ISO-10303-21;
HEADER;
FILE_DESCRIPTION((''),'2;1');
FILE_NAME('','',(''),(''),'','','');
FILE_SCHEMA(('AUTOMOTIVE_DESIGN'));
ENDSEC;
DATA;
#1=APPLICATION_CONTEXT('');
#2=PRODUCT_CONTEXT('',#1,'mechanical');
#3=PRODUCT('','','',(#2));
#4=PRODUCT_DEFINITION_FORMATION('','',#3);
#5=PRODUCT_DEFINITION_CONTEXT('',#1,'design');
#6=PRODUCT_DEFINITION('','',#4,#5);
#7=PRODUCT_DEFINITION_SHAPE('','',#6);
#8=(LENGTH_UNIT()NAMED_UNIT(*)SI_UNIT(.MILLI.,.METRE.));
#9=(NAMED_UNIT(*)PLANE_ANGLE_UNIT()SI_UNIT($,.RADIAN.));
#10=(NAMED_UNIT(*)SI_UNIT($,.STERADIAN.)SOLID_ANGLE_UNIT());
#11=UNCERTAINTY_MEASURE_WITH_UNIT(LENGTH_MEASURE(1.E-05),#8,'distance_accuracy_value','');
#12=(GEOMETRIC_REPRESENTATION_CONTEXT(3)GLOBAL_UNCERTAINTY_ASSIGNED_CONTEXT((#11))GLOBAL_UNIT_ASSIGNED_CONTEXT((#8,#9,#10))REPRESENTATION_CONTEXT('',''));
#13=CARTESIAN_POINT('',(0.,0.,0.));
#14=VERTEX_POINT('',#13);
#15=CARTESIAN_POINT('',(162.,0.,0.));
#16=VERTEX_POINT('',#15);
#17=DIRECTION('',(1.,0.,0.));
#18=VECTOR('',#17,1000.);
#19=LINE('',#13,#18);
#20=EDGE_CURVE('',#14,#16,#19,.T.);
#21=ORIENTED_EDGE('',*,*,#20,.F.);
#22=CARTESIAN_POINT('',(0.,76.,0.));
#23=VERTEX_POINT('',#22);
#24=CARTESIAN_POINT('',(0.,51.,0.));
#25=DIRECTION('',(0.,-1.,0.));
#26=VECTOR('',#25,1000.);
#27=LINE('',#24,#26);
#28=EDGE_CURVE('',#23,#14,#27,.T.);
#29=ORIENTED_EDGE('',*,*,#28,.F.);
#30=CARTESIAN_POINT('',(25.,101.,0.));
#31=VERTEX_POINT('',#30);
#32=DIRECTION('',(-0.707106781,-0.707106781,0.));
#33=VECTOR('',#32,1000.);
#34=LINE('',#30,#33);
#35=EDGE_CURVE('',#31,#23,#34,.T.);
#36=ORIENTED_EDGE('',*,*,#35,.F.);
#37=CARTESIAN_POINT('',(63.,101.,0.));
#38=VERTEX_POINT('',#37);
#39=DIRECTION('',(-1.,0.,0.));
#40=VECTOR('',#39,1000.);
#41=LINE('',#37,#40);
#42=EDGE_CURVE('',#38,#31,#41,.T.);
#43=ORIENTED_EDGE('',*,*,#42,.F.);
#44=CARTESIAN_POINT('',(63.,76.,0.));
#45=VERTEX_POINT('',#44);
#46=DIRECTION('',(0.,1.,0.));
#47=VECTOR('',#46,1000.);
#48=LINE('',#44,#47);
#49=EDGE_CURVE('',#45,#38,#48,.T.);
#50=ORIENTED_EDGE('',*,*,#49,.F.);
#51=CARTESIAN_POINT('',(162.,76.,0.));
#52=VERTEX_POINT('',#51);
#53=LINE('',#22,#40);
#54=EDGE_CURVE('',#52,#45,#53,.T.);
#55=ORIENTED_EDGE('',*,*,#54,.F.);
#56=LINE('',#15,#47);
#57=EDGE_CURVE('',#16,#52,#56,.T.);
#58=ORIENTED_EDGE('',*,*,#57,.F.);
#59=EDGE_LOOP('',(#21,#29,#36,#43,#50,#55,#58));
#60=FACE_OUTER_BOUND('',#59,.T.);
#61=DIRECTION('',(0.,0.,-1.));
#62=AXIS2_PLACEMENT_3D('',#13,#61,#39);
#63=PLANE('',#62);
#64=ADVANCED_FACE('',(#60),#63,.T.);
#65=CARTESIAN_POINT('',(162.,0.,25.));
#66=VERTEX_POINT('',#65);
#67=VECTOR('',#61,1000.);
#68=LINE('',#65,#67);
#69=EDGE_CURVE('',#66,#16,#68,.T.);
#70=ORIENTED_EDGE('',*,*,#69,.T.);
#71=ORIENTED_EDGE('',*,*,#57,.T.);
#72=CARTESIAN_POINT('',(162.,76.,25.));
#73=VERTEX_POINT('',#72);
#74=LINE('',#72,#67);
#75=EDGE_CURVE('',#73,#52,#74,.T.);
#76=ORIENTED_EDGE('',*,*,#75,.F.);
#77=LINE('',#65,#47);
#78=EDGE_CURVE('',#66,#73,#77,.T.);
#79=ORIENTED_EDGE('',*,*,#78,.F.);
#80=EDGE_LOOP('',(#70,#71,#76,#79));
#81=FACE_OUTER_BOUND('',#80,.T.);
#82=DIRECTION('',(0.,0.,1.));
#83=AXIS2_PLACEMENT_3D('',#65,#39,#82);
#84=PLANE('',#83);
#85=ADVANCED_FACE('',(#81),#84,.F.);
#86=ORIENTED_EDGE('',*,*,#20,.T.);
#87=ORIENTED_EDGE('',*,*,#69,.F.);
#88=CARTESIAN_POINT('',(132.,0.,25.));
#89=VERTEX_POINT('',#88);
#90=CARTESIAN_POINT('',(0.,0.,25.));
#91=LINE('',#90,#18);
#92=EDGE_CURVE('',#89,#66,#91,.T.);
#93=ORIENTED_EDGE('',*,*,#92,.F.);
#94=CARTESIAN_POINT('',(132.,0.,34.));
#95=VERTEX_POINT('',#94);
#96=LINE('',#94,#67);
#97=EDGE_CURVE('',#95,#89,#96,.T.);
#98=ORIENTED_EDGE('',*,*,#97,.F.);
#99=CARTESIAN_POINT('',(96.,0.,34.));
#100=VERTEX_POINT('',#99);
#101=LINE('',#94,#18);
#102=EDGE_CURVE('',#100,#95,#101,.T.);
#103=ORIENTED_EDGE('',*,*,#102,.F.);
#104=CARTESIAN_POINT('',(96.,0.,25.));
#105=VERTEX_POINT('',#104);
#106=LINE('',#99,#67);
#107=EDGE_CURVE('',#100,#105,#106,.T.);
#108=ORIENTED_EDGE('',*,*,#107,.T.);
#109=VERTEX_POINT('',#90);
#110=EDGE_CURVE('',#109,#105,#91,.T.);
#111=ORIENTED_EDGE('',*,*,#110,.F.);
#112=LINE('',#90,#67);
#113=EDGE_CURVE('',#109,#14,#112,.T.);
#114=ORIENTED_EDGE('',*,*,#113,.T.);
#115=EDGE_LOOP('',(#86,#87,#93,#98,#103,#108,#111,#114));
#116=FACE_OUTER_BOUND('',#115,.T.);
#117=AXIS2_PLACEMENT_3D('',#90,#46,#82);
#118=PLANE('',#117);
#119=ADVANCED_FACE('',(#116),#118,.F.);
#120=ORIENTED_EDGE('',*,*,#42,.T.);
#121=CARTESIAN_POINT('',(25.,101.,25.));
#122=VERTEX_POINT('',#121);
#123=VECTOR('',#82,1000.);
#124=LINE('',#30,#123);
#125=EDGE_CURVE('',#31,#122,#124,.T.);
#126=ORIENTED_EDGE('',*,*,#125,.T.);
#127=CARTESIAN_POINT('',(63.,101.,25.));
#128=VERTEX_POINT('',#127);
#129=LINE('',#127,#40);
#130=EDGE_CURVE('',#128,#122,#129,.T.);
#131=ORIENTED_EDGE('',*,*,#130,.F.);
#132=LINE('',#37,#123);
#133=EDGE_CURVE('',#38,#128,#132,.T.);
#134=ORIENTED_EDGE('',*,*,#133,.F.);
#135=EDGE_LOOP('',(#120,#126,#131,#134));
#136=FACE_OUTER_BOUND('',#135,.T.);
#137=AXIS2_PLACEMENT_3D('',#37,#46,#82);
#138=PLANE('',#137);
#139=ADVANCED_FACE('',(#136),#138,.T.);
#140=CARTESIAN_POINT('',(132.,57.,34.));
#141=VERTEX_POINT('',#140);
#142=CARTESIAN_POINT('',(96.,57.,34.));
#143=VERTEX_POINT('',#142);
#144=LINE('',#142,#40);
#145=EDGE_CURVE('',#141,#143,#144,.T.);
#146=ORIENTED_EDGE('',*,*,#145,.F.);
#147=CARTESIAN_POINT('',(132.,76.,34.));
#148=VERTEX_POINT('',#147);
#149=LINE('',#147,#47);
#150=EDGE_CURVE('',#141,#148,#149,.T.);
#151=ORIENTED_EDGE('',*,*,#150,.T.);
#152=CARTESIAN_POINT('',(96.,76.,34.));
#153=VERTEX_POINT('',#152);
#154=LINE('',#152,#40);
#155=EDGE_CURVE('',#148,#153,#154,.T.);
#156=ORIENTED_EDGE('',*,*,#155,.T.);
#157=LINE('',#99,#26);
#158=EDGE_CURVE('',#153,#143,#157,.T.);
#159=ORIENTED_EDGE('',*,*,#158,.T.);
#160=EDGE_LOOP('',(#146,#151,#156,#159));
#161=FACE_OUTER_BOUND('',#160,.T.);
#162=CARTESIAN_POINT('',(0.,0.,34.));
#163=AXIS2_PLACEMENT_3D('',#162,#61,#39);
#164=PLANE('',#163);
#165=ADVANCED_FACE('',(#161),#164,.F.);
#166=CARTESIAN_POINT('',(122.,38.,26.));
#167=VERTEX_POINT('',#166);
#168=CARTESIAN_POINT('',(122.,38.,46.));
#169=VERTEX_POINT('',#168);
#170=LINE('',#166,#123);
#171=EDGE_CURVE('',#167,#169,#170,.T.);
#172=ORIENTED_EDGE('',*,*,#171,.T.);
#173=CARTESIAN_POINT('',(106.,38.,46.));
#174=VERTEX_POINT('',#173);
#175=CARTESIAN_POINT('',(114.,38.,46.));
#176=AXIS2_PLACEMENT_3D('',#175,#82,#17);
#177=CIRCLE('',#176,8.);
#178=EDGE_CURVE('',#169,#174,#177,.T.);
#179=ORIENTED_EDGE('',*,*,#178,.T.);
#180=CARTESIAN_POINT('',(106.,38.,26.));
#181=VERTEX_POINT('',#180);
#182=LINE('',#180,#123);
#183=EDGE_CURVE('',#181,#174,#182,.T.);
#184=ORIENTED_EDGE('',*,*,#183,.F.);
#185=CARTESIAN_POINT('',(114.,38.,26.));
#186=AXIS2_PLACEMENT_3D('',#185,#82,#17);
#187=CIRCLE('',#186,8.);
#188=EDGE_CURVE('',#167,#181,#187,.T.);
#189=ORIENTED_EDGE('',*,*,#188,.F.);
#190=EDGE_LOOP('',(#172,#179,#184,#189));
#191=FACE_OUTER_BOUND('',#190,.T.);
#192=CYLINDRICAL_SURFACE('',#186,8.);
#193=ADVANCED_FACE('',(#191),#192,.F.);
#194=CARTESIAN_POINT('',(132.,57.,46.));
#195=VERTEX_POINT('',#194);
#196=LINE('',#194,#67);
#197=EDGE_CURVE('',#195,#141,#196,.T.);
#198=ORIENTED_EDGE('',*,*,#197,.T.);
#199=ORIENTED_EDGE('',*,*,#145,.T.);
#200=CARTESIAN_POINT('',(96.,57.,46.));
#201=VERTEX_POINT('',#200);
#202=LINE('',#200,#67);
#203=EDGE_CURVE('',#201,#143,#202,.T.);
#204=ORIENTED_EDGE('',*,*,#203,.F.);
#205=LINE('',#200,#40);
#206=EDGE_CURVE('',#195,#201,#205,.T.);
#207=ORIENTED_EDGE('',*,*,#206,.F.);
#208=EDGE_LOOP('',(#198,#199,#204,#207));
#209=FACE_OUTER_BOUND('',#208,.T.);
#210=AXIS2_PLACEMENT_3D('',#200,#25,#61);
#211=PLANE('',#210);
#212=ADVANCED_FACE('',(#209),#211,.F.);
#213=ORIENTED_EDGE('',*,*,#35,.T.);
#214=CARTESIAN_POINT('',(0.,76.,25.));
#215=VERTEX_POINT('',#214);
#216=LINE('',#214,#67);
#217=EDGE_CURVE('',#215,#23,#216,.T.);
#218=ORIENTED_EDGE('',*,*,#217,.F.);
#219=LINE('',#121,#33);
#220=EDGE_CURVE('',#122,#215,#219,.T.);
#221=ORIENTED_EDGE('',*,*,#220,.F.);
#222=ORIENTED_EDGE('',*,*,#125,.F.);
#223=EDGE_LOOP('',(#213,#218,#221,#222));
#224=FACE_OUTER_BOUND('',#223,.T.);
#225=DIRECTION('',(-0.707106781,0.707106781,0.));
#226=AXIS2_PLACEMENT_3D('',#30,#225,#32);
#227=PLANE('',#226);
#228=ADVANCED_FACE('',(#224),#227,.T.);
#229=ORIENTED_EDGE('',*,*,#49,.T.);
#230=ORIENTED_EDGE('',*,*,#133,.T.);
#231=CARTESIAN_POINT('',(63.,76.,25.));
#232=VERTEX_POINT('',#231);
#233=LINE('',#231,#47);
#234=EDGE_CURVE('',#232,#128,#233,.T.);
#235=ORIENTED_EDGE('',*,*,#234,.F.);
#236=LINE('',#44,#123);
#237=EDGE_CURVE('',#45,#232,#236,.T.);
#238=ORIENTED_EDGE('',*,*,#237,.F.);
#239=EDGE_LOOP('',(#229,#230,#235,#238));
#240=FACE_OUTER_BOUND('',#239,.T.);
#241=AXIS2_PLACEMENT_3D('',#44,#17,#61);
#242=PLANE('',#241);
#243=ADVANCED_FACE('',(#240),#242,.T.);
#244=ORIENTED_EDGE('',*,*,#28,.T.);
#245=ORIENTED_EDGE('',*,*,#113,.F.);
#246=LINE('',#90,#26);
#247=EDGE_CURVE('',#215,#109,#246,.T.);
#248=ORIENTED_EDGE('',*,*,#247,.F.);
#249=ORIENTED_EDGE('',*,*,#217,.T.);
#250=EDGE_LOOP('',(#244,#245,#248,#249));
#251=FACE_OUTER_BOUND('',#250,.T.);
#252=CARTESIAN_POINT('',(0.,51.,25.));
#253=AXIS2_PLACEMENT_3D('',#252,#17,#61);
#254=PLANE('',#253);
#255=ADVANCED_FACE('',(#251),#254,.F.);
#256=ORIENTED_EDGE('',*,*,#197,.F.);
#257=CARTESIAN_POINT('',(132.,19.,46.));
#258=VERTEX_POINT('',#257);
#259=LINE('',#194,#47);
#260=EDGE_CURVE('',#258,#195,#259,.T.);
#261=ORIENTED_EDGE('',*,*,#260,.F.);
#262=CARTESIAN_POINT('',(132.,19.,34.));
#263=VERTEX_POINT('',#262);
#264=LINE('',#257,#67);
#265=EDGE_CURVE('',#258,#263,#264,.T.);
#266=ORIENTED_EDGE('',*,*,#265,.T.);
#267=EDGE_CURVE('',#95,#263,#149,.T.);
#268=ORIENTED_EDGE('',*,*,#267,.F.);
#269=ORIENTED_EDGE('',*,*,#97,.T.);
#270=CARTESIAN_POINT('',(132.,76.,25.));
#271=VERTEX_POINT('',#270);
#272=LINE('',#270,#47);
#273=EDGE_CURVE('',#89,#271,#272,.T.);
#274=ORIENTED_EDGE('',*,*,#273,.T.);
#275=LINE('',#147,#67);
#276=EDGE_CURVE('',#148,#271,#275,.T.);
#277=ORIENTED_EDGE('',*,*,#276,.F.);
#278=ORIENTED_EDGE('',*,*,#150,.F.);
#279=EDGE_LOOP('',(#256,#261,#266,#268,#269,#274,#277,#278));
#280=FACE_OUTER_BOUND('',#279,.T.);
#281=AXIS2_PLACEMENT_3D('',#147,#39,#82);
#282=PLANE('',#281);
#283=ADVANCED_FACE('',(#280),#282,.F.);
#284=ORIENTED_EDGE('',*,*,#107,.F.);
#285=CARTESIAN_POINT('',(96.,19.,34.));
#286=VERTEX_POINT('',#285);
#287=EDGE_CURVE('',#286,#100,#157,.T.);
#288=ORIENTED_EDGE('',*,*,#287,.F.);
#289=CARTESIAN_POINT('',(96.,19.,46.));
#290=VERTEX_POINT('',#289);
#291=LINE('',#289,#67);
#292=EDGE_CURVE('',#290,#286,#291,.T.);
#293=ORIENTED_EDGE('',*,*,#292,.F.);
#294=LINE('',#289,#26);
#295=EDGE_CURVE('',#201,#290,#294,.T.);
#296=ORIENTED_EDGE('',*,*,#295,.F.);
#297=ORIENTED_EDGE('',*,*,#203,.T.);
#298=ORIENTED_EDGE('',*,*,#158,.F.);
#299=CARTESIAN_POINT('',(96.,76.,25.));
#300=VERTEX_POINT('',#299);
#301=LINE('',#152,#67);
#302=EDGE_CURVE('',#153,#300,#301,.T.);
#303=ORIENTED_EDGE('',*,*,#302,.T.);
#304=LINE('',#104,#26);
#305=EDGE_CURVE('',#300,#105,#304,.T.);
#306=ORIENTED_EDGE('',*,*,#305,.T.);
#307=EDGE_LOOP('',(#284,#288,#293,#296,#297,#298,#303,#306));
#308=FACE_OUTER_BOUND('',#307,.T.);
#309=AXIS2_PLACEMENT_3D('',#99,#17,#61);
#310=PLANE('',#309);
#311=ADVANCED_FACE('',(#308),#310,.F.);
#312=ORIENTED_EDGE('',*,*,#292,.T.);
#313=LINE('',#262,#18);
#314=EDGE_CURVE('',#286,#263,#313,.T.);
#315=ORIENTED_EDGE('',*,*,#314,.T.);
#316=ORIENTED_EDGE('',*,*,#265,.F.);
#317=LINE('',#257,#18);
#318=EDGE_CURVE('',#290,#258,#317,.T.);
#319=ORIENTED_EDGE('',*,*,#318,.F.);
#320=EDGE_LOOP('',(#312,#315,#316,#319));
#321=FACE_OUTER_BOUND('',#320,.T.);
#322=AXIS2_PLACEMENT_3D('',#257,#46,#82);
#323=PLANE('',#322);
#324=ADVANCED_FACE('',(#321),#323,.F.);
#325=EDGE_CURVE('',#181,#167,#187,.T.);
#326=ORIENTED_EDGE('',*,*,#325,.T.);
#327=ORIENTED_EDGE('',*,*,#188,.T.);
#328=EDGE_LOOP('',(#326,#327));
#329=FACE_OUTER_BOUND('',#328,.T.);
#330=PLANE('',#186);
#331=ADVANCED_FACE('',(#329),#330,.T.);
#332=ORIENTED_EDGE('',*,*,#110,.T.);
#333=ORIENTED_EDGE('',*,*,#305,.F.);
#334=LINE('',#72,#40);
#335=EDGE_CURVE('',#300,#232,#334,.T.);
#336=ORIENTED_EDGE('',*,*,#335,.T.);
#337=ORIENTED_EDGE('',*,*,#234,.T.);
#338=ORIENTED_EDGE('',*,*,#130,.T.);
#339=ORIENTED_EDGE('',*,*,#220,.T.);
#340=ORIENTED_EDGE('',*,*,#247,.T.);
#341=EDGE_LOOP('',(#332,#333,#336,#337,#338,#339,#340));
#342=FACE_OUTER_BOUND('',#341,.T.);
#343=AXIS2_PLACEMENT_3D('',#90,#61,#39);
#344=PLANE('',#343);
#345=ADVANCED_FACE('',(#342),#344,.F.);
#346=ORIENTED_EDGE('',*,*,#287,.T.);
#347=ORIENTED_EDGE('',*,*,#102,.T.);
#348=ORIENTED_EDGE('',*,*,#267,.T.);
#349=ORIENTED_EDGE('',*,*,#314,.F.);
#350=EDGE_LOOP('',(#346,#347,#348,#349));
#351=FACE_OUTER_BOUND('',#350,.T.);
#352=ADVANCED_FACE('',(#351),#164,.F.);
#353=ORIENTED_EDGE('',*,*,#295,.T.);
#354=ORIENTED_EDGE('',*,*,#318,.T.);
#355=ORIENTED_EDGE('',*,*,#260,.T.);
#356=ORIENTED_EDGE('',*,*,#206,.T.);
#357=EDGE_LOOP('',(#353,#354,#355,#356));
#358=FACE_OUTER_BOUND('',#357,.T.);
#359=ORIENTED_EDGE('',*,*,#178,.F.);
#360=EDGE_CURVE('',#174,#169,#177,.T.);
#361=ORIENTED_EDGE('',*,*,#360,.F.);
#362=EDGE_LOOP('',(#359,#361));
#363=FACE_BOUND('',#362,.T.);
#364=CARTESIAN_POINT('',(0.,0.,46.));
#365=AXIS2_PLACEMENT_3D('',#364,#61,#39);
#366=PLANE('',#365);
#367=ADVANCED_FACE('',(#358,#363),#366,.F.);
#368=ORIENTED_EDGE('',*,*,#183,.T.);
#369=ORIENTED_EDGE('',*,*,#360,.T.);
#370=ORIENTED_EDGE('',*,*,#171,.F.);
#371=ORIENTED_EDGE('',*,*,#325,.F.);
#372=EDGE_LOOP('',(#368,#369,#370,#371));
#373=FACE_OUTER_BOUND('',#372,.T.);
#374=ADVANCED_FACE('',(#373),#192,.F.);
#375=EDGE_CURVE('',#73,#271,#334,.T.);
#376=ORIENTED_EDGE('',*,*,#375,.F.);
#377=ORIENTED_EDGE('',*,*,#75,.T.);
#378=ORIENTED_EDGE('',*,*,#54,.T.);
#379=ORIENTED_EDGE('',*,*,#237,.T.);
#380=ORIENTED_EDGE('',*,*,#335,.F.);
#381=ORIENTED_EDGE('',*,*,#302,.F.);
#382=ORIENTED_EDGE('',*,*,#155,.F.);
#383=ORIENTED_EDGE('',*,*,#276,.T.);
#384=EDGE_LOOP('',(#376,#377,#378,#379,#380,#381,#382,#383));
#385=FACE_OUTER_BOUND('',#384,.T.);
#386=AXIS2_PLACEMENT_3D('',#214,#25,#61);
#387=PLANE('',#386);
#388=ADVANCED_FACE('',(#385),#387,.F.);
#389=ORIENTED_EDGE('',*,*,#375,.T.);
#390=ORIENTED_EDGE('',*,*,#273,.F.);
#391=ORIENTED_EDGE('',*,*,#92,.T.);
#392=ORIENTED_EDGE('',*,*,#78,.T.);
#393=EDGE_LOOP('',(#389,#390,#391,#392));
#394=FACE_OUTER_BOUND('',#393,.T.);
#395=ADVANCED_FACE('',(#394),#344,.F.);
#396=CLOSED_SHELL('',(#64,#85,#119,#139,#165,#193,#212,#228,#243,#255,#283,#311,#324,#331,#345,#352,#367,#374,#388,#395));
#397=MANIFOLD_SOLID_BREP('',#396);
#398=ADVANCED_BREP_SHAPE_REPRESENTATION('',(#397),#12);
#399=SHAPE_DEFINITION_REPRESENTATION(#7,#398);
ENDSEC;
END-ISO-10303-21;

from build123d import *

# Parameters (mm, degrees)
BASE_BLOCK_DEPTH   = 25
SIDE_BLOCK_DEPTH   = 25
PAD_SKETCH_W       = 36
PAD_SKETCH_H       = 76
MOUNTING_PAD_DEPTH = 9
LUG_BOSS_SKETCH_W  = 36
LUG_BOSS_SKETCH_H  = 38
LUG_BOSS_DEPTH     = 12
HOLE_SKETCH_16_R   = 8
HOLE_16_DEPTH      = 20


with BuildPart() as part:
    # Base Profile Sketch → Base Block (new body)
    with BuildSketch(Plane.XY):
        Polygon((0, 0), (162, 0), (162, 76), (25, 76), (0, 76), (0, 51), align=None)
    extrude(amount=BASE_BLOCK_DEPTH)

    # Side Block Sketch → Side Block (add)
    with BuildSketch(Plane.XY.offset(25)):
        Polygon((63, 76), (63, 101), (25, 101), (0, 76), (25, 76), align=None)
    extrude(amount=-SIDE_BLOCK_DEPTH)

    # Pad Sketch → Mounting Pad (add)
    with BuildSketch(Plane.XY.offset(25)):
        with Locations((114, 38)):
            Rectangle(PAD_SKETCH_W, PAD_SKETCH_H)
    extrude(amount=MOUNTING_PAD_DEPTH)

    # Lug Boss Sketch → Lug Boss (add)
    with BuildSketch(Plane.XY.offset(34)):
        with Locations((114, 38)):
            Rectangle(LUG_BOSS_SKETCH_W, LUG_BOSS_SKETCH_H)
    extrude(amount=LUG_BOSS_DEPTH)

    # Hole Sketch Ø16 → Hole Ø16 (cut)
    with BuildSketch(Plane.XY.offset(46)):
        with Locations((114, 38)):
            Circle(HOLE_SKETCH_16_R)
    extrude(amount=-HOLE_16_DEPTH, mode=Mode.SUBTRACT)


solid = part.part
